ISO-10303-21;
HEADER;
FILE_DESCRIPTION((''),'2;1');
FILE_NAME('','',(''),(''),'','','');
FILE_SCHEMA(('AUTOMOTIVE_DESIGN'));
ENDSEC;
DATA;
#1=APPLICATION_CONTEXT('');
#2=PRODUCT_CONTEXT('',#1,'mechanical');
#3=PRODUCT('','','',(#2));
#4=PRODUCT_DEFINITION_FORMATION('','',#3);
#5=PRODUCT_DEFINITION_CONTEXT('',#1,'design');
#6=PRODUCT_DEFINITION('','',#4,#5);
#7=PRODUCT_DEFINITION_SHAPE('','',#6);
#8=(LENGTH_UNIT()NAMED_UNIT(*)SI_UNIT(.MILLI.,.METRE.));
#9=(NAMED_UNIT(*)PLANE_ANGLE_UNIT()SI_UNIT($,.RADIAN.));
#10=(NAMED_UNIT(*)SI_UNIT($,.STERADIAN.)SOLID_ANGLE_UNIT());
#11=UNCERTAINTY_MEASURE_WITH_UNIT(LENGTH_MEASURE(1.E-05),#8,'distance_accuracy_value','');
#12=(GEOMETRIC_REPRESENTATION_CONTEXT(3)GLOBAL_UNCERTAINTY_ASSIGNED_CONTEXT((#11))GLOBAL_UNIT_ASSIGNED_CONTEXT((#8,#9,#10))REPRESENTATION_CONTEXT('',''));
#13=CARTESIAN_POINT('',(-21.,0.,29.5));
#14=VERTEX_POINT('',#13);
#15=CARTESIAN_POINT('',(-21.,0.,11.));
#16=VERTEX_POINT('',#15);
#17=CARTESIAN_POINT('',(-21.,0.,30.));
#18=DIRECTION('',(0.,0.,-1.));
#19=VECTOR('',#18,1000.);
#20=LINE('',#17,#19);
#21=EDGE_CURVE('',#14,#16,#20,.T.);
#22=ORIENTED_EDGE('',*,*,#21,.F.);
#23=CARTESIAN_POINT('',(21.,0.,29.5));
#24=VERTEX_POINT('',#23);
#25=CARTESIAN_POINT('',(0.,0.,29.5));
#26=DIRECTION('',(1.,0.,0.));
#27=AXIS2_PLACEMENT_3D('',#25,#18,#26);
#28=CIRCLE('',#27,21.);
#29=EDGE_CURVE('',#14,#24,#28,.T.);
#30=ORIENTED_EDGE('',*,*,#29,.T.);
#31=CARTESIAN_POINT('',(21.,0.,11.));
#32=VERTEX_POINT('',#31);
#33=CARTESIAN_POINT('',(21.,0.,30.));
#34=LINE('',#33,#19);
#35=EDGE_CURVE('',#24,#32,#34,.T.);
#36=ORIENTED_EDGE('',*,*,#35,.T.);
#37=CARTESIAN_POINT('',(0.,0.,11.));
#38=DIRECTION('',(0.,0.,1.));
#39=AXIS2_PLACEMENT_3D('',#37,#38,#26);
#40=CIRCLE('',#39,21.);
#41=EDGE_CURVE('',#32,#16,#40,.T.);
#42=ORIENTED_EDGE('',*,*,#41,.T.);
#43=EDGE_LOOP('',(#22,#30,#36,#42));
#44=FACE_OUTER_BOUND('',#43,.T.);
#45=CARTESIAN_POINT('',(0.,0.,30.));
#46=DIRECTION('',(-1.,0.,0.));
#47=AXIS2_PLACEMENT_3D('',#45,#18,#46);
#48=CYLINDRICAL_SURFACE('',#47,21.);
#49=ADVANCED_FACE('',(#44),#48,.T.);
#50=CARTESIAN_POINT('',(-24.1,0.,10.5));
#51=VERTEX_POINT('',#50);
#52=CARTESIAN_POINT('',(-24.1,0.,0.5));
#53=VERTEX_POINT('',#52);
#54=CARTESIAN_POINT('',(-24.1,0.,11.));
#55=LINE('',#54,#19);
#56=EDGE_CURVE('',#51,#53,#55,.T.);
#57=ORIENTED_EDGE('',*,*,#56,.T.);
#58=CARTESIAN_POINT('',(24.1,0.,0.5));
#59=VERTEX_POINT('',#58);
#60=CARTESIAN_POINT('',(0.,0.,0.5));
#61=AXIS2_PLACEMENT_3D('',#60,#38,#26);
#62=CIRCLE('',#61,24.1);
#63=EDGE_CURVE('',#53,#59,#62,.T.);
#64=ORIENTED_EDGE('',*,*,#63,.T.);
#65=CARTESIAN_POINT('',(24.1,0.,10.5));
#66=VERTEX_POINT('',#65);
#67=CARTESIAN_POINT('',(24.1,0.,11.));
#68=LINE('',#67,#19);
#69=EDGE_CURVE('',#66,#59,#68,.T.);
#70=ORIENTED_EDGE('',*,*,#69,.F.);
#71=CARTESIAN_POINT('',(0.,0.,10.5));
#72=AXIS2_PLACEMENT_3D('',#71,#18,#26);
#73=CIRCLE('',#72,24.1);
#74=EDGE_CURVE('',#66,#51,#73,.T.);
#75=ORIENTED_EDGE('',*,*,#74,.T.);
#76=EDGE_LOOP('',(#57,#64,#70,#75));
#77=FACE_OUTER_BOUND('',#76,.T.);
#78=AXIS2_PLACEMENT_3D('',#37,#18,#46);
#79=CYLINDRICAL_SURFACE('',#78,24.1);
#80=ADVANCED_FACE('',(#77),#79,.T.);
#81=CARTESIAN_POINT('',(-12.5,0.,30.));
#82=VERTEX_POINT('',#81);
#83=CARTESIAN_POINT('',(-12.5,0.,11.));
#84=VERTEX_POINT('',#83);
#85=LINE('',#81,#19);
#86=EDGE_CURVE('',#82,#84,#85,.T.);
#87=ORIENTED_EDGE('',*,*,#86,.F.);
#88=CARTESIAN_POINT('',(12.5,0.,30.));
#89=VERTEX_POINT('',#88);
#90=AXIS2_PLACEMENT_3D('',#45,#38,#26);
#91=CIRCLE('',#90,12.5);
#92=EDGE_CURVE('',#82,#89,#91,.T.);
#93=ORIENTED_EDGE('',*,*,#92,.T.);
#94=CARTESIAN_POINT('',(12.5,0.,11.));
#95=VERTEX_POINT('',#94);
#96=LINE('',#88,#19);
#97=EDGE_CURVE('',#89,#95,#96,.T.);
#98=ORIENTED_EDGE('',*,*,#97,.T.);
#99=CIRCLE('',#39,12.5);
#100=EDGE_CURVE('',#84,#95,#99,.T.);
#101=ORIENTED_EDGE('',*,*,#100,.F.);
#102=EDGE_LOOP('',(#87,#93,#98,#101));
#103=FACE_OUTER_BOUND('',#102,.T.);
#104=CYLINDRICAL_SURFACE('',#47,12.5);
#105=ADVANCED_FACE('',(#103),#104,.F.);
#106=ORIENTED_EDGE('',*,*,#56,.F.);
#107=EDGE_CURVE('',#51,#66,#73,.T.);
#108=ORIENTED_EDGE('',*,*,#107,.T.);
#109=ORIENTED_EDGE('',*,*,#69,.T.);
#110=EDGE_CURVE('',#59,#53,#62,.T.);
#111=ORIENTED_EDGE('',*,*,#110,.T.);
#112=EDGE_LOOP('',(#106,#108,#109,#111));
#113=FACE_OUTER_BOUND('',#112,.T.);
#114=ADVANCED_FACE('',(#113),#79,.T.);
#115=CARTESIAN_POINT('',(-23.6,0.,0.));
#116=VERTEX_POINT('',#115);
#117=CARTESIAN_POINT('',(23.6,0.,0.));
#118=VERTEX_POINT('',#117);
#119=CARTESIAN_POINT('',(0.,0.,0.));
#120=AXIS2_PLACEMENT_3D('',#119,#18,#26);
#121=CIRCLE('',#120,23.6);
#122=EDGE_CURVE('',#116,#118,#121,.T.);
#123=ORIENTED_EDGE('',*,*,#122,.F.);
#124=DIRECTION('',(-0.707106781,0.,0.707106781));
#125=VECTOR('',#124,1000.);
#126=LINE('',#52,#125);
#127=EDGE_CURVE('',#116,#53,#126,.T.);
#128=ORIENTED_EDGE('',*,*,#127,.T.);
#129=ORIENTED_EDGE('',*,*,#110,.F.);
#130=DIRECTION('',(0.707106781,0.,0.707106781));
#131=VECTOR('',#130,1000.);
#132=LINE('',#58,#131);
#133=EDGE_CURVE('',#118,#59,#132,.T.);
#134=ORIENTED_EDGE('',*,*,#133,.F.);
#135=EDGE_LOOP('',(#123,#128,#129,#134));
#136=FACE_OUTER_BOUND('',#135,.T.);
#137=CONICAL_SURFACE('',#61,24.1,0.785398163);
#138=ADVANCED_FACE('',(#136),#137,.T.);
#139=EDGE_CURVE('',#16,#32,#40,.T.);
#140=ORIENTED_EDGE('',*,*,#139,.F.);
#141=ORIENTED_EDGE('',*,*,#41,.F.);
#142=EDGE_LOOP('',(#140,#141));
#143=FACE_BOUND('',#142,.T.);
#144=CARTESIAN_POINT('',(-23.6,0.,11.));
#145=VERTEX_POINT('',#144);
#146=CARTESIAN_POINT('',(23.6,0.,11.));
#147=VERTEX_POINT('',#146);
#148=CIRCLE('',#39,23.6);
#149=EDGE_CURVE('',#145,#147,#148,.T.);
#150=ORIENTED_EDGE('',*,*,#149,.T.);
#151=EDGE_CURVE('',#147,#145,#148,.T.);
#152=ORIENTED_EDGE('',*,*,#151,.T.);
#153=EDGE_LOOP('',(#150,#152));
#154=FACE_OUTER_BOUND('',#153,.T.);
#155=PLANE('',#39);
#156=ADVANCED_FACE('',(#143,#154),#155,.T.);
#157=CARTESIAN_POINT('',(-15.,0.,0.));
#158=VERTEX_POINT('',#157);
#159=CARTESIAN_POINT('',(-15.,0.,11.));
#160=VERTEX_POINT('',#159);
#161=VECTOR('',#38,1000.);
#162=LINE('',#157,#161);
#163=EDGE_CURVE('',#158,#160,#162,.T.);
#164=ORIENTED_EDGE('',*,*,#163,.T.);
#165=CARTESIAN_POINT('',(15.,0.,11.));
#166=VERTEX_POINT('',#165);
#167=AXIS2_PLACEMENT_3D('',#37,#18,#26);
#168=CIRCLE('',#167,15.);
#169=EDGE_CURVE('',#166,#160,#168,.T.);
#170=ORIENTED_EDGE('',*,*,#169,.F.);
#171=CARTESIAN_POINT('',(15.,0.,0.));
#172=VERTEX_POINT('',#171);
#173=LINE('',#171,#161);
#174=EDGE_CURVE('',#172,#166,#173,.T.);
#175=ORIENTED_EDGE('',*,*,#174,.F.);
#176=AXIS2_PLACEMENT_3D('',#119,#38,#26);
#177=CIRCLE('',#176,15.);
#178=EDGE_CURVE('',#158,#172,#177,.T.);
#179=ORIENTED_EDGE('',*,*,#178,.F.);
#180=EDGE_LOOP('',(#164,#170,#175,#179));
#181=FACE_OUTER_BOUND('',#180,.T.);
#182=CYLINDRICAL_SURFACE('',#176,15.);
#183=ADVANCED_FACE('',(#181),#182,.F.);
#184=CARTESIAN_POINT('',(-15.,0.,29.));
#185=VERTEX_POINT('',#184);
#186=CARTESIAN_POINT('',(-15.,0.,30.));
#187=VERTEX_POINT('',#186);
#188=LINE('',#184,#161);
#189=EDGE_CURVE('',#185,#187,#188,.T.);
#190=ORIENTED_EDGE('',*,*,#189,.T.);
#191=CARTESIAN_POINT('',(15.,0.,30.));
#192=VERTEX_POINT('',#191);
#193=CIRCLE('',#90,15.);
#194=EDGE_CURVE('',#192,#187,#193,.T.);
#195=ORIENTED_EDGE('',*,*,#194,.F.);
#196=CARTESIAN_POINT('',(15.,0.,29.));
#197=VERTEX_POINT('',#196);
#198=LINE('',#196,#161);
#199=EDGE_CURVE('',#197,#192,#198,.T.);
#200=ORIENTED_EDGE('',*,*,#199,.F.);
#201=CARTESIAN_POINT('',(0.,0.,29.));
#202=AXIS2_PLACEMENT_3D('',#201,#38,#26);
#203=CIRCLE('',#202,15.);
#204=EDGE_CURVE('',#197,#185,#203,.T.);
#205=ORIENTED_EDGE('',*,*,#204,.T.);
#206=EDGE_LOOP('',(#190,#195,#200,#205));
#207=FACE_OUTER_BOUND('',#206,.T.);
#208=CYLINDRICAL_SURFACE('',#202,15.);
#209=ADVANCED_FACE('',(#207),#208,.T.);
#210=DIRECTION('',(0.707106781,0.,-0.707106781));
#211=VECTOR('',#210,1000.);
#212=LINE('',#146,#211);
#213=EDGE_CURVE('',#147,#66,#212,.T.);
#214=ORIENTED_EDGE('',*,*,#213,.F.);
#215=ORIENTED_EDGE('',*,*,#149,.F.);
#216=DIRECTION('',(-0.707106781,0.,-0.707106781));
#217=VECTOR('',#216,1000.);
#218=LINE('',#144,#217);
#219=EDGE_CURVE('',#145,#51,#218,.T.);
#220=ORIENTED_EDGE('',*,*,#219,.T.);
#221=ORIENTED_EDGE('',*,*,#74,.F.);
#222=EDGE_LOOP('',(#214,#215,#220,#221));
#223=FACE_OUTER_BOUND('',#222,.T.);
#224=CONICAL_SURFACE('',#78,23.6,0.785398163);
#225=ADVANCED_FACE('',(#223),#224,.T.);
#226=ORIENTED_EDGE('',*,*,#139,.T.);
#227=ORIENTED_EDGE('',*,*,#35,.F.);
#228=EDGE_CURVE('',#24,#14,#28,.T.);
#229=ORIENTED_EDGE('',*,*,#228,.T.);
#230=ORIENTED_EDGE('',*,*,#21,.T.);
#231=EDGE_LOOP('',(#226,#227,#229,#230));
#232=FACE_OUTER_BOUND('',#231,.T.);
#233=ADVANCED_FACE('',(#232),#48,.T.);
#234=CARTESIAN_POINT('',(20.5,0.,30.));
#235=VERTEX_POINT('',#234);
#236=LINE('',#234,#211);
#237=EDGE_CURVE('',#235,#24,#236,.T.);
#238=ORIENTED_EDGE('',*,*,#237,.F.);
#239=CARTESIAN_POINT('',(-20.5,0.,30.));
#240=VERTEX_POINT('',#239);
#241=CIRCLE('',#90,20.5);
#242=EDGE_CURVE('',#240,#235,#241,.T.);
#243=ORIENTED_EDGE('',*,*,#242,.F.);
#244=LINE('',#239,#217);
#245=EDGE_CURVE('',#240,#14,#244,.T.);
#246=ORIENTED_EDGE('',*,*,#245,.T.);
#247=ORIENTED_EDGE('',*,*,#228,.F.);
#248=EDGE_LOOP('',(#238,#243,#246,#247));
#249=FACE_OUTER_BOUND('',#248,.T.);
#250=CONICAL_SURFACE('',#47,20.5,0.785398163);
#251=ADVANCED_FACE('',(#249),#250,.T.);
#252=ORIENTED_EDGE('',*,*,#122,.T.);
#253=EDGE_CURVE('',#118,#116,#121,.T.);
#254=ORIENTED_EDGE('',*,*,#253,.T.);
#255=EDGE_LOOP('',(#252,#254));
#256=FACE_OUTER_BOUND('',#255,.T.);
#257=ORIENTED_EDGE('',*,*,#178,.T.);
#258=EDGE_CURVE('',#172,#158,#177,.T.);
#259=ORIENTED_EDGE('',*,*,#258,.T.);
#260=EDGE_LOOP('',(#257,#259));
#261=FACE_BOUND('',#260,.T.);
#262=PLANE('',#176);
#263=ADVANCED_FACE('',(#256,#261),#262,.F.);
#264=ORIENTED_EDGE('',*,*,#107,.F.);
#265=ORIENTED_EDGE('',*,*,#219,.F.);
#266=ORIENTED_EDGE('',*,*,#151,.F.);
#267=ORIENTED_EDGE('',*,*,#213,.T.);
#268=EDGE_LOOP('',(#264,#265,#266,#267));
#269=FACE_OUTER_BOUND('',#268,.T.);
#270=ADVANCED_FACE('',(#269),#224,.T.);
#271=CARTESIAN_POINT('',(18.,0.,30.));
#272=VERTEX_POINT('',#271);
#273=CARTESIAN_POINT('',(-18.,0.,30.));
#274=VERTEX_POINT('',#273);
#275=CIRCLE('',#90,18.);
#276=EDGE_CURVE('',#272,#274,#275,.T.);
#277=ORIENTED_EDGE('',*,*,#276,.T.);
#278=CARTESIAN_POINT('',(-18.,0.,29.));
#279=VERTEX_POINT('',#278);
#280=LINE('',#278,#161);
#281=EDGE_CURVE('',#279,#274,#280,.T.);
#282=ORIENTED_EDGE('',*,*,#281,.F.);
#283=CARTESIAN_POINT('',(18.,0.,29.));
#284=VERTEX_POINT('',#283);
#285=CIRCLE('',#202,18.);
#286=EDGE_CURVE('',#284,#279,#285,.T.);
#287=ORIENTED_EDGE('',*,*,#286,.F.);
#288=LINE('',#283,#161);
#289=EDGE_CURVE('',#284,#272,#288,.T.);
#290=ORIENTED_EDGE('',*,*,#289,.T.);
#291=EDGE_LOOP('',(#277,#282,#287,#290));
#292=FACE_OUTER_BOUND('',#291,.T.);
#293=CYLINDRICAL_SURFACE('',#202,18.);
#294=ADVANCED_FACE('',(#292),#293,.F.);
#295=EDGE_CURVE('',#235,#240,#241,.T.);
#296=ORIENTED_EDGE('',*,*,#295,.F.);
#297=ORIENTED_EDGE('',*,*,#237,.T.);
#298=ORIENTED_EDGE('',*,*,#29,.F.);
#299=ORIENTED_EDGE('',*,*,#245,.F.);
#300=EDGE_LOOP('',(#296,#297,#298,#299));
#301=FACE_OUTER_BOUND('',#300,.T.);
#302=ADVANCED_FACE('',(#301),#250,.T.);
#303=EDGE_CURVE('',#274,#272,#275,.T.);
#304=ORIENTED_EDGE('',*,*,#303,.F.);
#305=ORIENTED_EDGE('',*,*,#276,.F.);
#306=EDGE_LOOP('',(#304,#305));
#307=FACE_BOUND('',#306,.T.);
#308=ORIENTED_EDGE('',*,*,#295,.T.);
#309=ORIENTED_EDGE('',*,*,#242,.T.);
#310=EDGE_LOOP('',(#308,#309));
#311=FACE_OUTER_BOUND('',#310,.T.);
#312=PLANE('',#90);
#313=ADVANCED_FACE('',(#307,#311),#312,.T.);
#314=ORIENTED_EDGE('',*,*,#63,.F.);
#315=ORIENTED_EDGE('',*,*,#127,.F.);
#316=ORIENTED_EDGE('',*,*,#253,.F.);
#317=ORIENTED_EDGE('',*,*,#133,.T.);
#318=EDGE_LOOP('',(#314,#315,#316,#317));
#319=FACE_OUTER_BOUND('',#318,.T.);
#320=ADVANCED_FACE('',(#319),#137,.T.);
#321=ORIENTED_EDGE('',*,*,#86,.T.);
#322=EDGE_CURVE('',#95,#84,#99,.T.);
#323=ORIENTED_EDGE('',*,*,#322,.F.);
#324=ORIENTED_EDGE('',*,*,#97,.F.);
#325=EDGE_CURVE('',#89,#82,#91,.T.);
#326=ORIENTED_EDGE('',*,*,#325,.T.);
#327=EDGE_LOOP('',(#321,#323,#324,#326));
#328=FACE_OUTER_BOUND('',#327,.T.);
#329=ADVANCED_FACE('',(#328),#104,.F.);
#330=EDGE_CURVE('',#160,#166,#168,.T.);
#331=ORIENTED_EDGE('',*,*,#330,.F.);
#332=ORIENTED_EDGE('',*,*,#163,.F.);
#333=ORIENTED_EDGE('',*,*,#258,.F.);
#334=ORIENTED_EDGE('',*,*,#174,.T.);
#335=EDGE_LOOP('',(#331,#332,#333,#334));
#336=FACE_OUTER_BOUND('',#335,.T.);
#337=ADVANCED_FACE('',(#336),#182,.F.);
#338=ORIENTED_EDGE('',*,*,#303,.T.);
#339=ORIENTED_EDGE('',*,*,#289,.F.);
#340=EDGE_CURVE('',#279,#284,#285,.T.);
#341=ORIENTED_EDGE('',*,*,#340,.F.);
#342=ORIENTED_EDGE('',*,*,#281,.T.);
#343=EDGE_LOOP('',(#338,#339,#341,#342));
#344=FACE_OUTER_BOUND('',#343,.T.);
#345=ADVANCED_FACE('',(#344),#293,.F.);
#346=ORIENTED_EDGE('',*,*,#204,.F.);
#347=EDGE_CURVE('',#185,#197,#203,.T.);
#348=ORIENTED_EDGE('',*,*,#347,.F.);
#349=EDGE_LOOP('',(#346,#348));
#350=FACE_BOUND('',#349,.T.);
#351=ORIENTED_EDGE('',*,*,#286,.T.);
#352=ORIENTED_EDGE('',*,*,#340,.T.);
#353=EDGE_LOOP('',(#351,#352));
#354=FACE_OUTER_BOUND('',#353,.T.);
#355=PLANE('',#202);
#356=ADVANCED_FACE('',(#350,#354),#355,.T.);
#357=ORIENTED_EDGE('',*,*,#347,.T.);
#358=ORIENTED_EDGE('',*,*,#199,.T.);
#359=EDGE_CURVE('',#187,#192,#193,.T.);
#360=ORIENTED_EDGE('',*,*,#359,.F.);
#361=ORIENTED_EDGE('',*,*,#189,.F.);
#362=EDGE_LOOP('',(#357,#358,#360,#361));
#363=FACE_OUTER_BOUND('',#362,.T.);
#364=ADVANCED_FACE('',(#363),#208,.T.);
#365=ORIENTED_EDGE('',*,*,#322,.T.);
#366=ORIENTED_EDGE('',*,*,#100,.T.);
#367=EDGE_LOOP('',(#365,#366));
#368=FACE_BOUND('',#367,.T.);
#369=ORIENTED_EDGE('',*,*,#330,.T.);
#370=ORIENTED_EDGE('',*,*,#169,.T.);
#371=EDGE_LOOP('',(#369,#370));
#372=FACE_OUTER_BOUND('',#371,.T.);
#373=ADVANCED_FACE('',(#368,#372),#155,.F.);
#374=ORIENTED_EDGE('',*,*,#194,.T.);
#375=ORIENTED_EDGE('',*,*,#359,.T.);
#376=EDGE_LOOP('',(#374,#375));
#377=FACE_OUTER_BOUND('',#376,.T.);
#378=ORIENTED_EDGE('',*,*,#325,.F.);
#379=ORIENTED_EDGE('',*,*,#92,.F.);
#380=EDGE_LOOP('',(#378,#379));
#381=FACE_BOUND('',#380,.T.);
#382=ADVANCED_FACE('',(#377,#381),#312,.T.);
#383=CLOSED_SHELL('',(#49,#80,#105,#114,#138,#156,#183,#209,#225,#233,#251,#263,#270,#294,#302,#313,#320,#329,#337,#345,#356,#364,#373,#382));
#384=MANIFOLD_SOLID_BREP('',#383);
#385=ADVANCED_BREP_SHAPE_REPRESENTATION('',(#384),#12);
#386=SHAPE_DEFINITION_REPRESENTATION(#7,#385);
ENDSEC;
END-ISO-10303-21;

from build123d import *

# Parameters (mm, degrees)
SKETCH1_R           = 24.1
BOSS_EXTRUDE1_DEPTH = 11
SKETCH2_R           = 15
CUT_EXTRUDE1_DEPTH  = 36.813684535
SKETCH3_R           = 21
SKETCH3_R_2         = 12.5
BOSS_EXTRUDE2_DEPTH = 19
CHAMFER1_SIZE       = 0.5
SKETCH4_R           = 18
SKETCH4_R_2         = 15
CUT_EXTRUDE2_DEPTH  = 1


with BuildPart() as part:
    # Sketch1 → Boss-Extrude1 (new body)
    with BuildSketch(Plane.XY):
        Circle(SKETCH1_R)
    extrude(amount=BOSS_EXTRUDE1_DEPTH)

    # Sketch2 → Cut-Extrude1 (cut, through all)
    with BuildSketch(Plane.XY.offset(11)):
        Circle(SKETCH2_R)
    extrude(amount=-CUT_EXTRUDE1_DEPTH, mode=Mode.SUBTRACT)

    # Sketch3 → Boss-Extrude2 (add)
    with BuildSketch(Plane.XY.offset(11)):
        Circle(SKETCH3_R)
        Circle(SKETCH3_R_2, mode=Mode.SUBTRACT)
    extrude(amount=BOSS_EXTRUDE2_DEPTH)

    # Chamfer1
    chamfer1_edges = [part.edges().sort_by_distance(p)[0] for p in [
        (-21, 0, 30),
        (-24.1, 0, 0),
        (-24.1, 0, 11),
    ]]
    chamfer(chamfer1_edges, length=CHAMFER1_SIZE)

    # Sketch4 → Cut-Extrude2 (cut)
    with BuildSketch(Plane.XY.offset(30)):
        Circle(SKETCH4_R)
        Circle(SKETCH4_R_2, mode=Mode.SUBTRACT)
    extrude(amount=-CUT_EXTRUDE2_DEPTH, mode=Mode.SUBTRACT)


solid = part.part
